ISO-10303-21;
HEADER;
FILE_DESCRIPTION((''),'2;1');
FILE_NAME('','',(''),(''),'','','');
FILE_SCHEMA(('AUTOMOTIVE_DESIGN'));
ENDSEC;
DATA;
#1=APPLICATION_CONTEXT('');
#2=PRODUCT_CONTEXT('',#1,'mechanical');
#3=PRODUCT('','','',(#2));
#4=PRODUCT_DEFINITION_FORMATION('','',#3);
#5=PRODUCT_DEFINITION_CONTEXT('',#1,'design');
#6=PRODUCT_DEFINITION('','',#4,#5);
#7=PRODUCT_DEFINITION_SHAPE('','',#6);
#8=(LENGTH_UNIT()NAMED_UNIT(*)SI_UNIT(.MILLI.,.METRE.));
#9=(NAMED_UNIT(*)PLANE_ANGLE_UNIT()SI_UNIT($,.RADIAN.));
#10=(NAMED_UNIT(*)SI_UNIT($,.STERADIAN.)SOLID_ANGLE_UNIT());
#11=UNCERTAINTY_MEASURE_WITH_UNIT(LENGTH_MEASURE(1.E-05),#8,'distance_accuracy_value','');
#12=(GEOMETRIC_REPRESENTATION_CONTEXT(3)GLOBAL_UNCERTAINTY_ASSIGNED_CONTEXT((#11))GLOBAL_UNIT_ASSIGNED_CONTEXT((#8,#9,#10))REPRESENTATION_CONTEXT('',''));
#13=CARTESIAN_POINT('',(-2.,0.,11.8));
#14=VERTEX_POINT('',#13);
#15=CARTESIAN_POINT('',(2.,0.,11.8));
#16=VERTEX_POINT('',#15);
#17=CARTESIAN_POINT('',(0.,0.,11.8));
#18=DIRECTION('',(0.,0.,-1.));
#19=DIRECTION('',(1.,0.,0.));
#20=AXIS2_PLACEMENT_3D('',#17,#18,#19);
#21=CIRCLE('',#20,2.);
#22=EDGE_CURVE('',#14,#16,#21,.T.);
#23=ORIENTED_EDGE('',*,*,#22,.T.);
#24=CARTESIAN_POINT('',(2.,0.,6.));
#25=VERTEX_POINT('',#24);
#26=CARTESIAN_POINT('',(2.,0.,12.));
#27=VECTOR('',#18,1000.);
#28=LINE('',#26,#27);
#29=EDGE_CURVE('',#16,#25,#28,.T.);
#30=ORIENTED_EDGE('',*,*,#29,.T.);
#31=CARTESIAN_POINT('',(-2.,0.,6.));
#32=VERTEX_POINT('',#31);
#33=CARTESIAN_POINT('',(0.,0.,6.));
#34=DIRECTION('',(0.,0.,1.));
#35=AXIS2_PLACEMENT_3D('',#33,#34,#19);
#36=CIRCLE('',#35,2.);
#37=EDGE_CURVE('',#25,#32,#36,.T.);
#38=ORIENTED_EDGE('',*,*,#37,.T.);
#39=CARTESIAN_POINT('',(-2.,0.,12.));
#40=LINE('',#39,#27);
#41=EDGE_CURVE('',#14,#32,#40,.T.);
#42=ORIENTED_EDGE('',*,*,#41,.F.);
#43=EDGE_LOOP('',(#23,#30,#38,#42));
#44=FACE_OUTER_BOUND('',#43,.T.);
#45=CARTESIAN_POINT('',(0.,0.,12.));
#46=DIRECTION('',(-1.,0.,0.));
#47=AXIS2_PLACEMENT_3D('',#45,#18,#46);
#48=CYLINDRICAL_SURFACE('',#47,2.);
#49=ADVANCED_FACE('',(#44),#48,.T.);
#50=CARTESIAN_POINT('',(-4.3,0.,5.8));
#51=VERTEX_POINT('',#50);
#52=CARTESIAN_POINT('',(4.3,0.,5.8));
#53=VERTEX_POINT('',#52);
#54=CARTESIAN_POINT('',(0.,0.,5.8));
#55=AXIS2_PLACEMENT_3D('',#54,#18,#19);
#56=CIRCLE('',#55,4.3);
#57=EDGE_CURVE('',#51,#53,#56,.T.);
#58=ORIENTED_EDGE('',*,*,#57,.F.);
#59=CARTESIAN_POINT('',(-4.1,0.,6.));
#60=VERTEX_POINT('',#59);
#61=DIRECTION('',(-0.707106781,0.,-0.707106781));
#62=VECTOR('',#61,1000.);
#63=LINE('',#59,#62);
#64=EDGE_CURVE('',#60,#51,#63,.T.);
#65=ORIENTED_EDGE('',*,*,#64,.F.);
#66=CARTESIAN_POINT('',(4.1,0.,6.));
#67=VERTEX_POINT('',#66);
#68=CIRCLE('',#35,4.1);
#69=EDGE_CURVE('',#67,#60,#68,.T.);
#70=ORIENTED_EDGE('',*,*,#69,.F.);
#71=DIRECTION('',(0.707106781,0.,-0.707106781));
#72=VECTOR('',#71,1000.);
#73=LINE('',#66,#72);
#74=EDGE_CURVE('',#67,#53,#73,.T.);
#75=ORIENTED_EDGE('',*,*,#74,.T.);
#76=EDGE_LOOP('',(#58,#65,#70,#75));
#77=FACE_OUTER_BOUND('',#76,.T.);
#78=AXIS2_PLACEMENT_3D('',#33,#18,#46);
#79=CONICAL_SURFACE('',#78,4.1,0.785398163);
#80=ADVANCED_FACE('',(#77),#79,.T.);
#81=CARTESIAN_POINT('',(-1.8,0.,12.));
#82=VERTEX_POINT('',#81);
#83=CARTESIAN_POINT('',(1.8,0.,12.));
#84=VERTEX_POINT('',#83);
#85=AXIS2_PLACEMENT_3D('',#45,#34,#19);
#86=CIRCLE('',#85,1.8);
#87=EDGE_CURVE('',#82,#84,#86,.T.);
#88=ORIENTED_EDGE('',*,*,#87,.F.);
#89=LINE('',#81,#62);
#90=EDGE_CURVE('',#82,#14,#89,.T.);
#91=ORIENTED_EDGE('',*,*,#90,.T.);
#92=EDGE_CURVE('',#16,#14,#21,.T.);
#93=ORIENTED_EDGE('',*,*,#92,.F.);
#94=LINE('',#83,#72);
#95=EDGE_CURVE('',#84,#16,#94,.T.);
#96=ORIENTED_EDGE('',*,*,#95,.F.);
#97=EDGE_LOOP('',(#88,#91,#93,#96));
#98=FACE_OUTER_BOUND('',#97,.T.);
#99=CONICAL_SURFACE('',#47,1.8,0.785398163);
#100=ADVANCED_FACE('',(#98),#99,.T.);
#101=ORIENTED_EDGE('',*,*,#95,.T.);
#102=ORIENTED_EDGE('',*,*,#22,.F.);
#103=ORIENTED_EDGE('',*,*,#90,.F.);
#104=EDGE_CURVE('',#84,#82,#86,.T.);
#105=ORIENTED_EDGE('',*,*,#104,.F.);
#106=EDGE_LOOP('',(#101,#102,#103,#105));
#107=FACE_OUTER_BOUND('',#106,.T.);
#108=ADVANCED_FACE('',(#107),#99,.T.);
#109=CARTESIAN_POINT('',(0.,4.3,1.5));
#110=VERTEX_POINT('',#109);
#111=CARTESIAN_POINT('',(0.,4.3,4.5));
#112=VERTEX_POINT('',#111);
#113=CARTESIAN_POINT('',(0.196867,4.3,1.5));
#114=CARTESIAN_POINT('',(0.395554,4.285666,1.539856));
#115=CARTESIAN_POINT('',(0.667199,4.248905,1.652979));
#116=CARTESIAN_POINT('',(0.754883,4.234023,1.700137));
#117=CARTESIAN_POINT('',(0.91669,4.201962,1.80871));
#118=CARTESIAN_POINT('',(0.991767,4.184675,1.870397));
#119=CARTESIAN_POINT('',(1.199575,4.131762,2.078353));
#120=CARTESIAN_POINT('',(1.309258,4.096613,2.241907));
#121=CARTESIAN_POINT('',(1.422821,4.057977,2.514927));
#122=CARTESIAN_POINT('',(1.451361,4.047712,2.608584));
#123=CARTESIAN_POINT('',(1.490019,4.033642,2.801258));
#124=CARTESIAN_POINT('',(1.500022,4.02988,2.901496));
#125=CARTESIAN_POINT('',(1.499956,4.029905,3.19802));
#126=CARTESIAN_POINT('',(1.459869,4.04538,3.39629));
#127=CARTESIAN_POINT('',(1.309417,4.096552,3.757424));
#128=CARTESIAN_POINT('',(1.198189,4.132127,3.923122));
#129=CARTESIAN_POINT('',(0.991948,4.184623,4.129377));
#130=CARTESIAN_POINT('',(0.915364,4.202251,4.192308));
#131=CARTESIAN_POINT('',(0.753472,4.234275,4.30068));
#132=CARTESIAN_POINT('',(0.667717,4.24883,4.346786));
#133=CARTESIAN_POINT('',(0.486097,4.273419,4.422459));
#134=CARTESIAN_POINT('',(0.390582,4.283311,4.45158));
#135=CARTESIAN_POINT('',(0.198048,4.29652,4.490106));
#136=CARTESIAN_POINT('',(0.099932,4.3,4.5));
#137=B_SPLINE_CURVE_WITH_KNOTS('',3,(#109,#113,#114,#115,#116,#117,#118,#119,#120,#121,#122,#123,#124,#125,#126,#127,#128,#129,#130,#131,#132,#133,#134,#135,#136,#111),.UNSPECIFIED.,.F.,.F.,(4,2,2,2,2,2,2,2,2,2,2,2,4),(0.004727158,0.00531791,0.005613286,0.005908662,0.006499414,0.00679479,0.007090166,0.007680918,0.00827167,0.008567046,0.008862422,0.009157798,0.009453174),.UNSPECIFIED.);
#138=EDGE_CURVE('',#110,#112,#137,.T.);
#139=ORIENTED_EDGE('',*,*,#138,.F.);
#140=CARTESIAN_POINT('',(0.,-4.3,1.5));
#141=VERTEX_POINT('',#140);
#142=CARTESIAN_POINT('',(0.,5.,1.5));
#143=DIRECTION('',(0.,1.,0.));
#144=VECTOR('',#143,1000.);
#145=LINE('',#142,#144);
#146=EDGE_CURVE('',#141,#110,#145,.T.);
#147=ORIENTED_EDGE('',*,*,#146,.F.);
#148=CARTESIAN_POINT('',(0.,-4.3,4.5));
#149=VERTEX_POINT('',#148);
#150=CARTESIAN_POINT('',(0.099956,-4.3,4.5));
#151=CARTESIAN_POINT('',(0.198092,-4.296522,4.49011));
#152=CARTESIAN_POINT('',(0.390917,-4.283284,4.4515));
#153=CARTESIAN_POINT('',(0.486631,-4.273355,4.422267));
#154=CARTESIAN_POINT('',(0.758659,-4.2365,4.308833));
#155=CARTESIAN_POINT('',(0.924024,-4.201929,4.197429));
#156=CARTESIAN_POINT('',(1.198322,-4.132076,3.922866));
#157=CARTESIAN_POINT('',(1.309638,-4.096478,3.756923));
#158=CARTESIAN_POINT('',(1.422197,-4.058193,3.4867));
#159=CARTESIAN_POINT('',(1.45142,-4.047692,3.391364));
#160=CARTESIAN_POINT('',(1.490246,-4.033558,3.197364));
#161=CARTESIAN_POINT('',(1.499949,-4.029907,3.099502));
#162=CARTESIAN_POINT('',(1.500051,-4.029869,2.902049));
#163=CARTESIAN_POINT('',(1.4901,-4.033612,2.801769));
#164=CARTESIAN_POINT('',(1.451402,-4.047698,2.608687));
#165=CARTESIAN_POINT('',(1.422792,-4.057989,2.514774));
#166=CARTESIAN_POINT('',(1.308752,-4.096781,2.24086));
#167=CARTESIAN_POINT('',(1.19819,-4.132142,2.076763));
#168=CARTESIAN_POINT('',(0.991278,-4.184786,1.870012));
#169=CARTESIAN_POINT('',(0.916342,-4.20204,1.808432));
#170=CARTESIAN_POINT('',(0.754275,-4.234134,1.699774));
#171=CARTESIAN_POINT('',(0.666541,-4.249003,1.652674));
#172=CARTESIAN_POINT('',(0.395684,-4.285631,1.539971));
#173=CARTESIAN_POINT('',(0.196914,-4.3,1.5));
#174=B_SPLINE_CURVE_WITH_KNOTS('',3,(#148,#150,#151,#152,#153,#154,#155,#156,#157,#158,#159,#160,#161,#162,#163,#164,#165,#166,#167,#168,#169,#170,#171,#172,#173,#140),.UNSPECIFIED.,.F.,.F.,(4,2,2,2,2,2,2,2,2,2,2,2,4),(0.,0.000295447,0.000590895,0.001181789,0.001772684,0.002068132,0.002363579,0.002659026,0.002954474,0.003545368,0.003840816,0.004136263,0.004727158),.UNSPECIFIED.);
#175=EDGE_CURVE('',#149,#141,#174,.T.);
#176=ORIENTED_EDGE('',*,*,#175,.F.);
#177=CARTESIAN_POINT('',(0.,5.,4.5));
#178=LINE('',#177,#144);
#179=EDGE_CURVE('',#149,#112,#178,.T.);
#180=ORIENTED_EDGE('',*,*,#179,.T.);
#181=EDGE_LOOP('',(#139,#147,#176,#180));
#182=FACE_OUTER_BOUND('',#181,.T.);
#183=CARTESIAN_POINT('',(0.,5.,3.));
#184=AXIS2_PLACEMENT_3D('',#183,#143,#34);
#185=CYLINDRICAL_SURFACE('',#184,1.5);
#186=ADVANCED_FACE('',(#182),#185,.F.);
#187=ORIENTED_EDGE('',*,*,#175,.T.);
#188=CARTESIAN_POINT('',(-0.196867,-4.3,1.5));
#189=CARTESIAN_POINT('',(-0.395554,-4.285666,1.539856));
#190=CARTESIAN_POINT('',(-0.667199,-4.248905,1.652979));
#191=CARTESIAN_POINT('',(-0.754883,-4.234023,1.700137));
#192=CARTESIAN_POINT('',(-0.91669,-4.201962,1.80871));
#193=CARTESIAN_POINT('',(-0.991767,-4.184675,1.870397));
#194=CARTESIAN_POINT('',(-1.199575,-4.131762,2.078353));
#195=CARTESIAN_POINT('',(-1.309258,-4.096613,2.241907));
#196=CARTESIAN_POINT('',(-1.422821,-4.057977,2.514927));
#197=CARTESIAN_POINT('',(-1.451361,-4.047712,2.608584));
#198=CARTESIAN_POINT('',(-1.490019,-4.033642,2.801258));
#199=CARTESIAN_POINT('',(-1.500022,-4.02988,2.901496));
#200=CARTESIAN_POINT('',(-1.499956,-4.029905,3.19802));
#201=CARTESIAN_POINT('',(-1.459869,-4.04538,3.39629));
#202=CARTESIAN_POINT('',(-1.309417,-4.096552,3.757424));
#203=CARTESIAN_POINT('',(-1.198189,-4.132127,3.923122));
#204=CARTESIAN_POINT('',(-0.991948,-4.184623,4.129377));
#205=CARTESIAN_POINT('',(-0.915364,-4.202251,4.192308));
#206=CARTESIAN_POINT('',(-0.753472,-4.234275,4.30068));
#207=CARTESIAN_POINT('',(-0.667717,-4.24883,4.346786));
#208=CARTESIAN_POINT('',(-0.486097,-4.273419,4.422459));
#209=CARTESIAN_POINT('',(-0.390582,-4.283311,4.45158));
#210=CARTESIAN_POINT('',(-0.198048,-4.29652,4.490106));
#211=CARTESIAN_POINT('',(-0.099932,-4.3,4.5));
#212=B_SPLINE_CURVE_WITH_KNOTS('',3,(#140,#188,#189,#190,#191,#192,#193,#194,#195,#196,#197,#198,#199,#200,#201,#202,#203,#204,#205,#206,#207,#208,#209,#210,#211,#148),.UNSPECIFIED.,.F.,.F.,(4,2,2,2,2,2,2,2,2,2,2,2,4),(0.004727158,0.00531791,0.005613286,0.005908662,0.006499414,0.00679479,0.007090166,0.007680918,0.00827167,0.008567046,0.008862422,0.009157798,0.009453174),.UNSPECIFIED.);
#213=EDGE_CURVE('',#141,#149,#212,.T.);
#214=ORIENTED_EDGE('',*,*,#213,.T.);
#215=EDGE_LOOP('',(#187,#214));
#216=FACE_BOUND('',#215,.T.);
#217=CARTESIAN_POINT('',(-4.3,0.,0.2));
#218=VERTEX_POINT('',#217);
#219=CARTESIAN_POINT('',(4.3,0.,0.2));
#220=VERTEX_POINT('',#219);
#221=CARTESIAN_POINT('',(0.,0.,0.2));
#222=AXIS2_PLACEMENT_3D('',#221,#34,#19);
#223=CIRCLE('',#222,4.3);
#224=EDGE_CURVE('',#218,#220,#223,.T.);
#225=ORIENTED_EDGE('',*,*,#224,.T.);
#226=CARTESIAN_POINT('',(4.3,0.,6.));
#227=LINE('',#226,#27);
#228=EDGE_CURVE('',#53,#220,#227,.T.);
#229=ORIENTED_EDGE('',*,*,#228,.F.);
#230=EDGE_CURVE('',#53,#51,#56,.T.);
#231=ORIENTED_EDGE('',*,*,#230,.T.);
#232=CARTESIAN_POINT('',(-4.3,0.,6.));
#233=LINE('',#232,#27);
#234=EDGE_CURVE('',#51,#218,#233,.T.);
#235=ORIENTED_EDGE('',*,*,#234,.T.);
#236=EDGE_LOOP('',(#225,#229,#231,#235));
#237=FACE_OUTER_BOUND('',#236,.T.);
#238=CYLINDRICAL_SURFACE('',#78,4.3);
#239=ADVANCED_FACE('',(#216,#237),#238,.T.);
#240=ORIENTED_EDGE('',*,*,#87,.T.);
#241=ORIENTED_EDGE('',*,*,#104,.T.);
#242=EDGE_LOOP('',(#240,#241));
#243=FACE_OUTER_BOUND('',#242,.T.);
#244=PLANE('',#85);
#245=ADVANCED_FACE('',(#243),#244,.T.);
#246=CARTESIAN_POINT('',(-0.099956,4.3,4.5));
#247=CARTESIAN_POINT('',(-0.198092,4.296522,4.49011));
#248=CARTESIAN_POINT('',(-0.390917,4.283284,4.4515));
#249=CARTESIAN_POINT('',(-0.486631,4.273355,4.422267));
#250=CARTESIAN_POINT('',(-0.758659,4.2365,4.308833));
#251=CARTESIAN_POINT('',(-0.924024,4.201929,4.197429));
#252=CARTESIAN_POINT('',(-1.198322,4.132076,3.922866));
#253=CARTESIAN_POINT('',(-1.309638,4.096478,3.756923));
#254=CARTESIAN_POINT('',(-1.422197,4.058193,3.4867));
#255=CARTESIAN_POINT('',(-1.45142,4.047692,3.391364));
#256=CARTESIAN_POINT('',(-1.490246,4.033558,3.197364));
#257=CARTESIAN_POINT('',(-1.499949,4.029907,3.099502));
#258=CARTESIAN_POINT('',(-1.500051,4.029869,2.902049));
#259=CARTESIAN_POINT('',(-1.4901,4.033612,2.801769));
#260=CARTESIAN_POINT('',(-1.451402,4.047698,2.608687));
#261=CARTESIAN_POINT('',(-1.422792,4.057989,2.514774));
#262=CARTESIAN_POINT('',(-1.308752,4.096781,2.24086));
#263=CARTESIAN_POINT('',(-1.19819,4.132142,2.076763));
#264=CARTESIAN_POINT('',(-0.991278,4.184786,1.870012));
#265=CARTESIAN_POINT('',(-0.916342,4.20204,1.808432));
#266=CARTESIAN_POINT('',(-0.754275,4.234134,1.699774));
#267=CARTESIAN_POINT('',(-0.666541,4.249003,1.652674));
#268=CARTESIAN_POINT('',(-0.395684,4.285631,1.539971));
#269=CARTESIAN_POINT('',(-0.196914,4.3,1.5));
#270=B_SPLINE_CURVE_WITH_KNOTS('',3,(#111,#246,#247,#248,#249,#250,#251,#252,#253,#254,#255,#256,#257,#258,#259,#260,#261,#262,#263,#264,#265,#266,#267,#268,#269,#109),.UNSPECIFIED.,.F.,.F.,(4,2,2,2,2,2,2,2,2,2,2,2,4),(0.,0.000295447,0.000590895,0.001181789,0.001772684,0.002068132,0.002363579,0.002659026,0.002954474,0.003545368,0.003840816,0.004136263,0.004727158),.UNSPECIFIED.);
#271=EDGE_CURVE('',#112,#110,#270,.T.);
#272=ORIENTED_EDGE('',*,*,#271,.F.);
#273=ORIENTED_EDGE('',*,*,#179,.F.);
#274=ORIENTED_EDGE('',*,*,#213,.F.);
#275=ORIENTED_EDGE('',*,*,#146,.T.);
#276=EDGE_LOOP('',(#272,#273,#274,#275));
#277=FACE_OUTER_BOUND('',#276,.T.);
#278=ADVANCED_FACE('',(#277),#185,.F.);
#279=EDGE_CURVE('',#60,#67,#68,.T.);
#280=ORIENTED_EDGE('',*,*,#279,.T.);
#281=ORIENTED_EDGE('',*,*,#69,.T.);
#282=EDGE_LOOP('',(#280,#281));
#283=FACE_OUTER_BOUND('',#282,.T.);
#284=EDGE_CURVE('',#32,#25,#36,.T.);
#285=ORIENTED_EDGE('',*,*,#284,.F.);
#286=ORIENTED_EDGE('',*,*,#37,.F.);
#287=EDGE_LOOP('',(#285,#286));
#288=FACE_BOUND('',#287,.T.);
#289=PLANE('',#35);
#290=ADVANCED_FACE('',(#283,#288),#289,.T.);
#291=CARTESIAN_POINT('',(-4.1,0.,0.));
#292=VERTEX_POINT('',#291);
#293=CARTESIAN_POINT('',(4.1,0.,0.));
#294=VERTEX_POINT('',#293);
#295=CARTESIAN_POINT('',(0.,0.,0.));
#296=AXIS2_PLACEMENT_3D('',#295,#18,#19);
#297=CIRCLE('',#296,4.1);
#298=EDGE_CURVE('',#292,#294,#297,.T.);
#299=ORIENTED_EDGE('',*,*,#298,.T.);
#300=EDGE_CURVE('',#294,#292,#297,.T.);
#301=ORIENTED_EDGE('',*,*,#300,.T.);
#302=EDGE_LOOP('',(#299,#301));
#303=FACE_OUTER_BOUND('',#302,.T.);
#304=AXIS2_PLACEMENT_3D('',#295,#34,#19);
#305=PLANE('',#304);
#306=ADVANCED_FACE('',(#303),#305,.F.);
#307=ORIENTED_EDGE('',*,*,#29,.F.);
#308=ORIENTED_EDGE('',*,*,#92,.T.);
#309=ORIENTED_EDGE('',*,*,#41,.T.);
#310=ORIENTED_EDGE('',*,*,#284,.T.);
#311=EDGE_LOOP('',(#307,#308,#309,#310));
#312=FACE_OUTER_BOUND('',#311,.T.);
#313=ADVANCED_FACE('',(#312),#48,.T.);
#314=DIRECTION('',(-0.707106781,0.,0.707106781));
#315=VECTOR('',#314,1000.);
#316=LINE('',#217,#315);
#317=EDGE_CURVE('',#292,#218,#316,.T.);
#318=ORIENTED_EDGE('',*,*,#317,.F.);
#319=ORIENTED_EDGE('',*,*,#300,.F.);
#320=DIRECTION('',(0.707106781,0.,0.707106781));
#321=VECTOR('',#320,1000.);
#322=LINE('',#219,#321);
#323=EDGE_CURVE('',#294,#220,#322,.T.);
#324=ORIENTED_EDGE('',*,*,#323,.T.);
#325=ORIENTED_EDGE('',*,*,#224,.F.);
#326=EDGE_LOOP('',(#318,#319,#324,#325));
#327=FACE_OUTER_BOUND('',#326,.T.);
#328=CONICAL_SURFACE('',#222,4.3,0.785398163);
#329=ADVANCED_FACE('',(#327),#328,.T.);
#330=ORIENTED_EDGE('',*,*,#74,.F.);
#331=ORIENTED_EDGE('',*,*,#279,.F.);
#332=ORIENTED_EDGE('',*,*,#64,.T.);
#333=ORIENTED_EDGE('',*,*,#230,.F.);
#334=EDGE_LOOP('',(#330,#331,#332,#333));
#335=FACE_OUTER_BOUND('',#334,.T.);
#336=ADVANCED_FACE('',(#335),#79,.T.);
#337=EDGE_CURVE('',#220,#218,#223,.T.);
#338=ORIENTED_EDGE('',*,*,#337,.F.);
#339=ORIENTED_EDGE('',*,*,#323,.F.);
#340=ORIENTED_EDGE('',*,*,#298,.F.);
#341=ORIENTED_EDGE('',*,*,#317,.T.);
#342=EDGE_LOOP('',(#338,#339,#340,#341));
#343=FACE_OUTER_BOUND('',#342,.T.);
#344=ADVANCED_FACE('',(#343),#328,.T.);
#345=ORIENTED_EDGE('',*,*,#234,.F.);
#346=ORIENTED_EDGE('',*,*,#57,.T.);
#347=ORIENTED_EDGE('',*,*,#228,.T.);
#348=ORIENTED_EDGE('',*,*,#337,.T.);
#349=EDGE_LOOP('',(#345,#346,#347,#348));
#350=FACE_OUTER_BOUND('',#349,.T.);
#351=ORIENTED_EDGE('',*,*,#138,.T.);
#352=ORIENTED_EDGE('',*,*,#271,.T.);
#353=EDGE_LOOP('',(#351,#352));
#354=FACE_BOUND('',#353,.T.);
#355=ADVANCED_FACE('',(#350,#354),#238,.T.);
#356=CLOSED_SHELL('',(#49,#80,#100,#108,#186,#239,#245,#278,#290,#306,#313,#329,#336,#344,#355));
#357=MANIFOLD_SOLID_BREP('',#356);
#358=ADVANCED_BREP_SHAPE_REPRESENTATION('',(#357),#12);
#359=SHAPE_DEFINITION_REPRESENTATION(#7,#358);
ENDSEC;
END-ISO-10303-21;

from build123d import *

# Parameters (mm, degrees)
SKETCH1_R                = 4.3
BOSS_EXTRUDE1_DEPTH      = 6
SKETCH2_R                = 2
BOSS_EXTRUDE2_DEPTH      = 6
CHAMFER1_SIZE            = 0.2
F_3_0_3_DIAMETER_HOLE1_D = 3


with BuildPart() as part:
    # Sketch1 → Boss-Extrude1 (new body)
    with BuildSketch(Plane.XY):
        Circle(SKETCH1_R)
    extrude(amount=BOSS_EXTRUDE1_DEPTH)

    # Sketch2 → Boss-Extrude2 (add)
    with BuildSketch(Plane.XY.offset(6)):
        Circle(SKETCH2_R)
    extrude(amount=BOSS_EXTRUDE2_DEPTH)

    # Chamfer1
    chamfer1_edges = [part.edges().sort_by_distance(p)[0] for p in [
        (-4.3, 0, 0),
        (-4.3, 0, 6),
        (-2, 0, 12),
    ]]
    chamfer(chamfer1_edges, length=CHAMFER1_SIZE)

    # Ø3.0 (3) Diameter Hole1 (through all)
    with Locations(Plane(origin=(0, 5, 0), x_dir=(1, 0, 0), z_dir=(0, 1, 0))):
        with Locations((0, -3)):
            Hole(F_3_0_3_DIAMETER_HOLE1_D / 2)


solid = part.part
